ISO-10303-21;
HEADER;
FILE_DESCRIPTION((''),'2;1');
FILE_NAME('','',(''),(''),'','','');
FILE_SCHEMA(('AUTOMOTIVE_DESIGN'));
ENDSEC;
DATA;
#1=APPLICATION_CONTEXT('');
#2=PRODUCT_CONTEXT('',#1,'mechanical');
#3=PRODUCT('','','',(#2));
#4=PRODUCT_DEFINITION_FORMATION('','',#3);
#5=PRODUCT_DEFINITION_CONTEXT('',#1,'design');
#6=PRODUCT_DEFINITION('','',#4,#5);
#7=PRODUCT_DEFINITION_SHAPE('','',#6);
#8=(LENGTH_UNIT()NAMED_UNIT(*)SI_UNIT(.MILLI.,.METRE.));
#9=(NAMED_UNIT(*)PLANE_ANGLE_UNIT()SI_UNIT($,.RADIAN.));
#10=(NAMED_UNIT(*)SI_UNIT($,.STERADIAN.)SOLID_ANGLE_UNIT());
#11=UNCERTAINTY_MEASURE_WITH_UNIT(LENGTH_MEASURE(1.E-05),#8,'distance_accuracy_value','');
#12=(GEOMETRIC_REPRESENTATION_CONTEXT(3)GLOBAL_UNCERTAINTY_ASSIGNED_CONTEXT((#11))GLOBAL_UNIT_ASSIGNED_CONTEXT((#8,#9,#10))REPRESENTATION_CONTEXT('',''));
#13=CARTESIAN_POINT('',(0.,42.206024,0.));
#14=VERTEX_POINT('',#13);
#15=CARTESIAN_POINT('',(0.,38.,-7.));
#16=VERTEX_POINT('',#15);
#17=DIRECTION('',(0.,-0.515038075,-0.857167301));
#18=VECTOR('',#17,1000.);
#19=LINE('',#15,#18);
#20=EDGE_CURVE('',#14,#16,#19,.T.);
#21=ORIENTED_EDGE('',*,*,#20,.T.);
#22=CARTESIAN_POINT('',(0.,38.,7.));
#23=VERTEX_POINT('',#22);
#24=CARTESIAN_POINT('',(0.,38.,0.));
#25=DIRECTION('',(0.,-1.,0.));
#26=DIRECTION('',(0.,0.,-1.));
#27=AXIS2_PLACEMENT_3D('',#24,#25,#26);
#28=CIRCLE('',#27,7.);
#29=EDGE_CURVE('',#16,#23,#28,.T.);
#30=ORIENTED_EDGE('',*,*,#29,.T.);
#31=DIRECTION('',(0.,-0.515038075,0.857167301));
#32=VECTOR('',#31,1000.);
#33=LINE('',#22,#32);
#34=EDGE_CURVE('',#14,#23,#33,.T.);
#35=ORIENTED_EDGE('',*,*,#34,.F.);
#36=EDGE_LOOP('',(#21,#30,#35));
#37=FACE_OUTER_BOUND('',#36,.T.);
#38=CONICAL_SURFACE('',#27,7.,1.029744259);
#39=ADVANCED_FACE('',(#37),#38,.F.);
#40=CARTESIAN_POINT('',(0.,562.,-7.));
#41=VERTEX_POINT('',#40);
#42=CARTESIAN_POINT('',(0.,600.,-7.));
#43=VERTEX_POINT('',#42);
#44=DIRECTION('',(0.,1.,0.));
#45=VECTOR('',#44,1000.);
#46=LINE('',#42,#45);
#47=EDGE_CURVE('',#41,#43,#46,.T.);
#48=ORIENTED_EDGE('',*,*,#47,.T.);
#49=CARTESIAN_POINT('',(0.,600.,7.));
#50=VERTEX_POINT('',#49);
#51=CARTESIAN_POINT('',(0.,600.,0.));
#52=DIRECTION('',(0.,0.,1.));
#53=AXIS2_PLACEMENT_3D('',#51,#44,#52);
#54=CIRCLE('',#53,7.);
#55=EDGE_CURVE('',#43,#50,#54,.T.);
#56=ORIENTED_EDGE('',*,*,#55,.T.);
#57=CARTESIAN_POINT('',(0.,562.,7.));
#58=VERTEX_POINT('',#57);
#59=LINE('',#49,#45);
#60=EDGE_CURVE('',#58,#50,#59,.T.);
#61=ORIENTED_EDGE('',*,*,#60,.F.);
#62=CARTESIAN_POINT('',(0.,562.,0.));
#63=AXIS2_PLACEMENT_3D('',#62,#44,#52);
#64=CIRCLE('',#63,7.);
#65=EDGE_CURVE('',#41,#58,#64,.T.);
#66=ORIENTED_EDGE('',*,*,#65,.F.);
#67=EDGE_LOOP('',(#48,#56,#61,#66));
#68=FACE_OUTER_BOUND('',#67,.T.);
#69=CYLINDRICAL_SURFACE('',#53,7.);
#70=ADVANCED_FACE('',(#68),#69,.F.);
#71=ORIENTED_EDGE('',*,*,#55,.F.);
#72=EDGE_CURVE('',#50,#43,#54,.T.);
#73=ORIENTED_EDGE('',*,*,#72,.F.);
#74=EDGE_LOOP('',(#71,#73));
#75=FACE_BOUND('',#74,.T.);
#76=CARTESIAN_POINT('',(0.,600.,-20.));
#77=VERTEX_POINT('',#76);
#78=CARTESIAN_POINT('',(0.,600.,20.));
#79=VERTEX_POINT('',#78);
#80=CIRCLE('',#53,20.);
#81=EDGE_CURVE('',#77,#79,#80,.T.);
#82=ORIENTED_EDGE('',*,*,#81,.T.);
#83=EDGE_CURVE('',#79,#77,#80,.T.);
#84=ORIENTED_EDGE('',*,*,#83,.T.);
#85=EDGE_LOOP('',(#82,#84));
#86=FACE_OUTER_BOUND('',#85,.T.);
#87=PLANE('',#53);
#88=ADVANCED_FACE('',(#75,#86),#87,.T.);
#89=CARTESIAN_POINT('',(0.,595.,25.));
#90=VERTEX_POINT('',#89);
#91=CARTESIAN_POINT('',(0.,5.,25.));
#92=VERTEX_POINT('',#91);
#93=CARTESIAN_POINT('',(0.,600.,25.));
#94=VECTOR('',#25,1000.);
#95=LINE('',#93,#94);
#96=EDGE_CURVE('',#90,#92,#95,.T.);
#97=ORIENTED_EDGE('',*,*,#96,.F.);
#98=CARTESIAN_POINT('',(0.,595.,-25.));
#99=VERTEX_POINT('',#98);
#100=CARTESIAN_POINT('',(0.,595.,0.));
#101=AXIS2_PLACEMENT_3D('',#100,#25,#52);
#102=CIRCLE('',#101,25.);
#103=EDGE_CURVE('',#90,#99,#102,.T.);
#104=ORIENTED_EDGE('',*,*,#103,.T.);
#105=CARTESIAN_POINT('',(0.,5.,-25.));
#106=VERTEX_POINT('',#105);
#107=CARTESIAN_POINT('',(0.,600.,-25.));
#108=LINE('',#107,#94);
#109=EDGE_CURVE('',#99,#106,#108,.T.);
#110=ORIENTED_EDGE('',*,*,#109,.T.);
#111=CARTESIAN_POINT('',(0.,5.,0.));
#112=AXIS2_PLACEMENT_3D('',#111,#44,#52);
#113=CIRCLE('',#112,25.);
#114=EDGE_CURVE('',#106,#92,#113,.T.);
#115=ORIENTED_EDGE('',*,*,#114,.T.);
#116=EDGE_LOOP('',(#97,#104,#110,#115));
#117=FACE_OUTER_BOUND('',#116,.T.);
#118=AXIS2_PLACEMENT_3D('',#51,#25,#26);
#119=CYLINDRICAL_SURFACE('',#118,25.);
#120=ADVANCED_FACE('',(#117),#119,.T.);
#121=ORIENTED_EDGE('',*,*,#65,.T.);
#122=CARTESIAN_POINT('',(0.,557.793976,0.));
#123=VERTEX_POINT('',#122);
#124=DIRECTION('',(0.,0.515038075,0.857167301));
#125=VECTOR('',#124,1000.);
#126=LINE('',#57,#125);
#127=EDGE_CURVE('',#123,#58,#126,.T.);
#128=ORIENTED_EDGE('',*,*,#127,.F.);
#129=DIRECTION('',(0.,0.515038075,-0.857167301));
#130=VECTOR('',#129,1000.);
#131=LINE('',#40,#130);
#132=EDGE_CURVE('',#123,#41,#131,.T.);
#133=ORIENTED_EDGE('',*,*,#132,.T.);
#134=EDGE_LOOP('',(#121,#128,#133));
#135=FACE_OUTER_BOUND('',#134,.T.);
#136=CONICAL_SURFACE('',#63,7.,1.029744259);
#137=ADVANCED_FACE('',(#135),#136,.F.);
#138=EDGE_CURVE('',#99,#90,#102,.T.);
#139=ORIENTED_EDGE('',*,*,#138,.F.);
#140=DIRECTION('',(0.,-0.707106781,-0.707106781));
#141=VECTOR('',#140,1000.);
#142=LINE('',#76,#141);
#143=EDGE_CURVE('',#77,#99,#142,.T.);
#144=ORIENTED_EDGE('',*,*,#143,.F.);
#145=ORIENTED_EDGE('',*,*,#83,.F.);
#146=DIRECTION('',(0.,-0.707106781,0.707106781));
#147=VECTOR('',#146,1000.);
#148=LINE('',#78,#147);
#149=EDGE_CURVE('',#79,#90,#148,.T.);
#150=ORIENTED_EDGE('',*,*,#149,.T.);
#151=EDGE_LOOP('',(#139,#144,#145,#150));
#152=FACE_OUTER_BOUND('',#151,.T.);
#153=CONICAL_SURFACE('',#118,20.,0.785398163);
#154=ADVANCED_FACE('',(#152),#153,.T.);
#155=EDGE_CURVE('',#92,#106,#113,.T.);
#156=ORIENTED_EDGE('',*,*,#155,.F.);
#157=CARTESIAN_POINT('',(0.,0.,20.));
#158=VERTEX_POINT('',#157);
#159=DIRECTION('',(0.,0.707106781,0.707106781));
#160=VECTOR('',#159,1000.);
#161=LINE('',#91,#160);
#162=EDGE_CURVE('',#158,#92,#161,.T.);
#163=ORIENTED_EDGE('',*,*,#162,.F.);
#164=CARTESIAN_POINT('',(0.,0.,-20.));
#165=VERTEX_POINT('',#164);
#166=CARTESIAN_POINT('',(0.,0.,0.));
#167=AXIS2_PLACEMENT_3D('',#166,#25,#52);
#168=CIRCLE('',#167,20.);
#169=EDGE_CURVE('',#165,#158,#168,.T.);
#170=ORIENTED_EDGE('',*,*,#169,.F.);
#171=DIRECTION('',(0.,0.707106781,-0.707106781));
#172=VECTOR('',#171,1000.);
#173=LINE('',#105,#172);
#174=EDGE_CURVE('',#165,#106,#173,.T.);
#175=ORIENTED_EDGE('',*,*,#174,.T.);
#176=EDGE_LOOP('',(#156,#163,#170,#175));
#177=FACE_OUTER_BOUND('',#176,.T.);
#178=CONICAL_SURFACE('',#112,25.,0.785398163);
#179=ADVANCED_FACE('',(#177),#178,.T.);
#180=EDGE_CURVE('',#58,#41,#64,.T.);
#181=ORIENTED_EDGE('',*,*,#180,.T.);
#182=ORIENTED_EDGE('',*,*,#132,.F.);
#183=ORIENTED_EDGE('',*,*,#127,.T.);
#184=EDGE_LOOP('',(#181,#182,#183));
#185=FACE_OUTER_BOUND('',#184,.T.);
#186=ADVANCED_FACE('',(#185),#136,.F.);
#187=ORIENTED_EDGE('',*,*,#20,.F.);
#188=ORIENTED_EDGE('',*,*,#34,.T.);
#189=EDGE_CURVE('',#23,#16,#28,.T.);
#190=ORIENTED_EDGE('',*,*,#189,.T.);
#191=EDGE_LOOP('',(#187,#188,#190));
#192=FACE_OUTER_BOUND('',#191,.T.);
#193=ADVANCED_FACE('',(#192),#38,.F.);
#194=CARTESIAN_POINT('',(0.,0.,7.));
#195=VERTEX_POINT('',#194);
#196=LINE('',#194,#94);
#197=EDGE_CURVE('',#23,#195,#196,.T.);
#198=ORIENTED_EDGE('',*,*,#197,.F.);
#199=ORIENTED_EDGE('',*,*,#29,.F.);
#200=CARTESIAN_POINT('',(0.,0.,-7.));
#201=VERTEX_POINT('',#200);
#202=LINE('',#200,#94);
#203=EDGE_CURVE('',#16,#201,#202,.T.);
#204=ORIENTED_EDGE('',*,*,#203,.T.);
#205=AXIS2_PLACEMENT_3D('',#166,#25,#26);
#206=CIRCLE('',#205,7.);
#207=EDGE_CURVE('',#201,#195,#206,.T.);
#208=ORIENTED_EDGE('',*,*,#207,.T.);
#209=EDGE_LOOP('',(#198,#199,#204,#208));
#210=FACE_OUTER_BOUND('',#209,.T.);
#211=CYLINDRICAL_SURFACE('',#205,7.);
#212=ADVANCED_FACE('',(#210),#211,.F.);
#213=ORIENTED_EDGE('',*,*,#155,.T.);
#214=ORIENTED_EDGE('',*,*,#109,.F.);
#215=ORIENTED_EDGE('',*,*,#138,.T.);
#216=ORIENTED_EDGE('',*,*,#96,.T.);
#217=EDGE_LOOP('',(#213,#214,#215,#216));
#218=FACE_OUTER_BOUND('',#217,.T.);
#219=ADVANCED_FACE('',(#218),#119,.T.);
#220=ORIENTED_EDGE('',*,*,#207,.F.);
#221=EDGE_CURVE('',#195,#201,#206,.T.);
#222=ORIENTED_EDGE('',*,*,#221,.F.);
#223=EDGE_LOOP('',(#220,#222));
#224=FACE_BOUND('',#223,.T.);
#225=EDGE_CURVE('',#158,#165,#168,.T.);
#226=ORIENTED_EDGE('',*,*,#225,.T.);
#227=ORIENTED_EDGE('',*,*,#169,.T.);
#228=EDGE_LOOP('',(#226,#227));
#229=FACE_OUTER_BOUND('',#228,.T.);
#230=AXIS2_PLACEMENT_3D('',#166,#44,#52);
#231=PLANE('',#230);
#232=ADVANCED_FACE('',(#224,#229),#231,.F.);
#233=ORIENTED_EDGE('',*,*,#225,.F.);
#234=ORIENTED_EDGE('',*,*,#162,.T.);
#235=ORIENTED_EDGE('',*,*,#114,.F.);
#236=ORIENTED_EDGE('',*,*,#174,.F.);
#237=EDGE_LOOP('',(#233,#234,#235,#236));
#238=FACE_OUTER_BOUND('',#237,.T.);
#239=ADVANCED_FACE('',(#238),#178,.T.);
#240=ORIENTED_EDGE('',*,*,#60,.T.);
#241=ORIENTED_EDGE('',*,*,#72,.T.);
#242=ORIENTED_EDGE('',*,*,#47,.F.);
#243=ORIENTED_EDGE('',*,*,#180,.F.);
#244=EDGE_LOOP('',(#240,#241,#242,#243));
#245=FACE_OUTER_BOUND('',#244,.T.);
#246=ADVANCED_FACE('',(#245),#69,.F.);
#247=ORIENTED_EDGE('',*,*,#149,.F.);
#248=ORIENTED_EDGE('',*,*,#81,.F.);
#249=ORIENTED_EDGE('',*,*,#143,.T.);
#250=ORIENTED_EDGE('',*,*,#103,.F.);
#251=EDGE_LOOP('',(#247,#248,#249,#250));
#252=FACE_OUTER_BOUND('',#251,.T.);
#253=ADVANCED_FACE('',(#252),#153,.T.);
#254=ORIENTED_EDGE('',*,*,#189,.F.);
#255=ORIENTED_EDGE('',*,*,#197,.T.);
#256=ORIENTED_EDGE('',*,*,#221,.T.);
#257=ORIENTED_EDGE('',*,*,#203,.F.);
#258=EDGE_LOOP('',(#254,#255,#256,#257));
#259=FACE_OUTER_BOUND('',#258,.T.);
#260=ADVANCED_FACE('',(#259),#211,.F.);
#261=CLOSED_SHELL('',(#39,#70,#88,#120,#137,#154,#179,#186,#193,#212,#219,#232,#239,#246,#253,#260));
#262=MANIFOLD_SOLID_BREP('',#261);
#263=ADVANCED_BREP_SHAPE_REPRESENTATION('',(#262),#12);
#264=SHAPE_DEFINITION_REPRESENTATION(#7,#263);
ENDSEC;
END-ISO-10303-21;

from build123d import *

# Parameters (mm, degrees)
SKETCH1_R              = 25
BOSS_EXTRUDE1_DEPTH    = 600
CHAMFER1_SIZE          = 5
M16_TAPPED_HOLE1_D     = 14
M16_TAPPED_HOLE1_DEPTH = 38
M16_TAPPED_HOLE1_TIP   = 4.206024333
M16_TAPPED_HOLE2_D     = 14
M16_TAPPED_HOLE2_DEPTH = 38
M16_TAPPED_HOLE2_TIP   = 4.206024333


with BuildPart() as part:
    # Sketch1 → Boss-Extrude1 (new body)
    with BuildSketch(Plane(origin=(0, 0, 0), x_dir=(1, 0, 0), z_dir=(0, 1, 0))):
        with Locations(Location((0, 0, 0), (0, 0, 270))):
            Circle(SKETCH1_R)
    extrude(amount=BOSS_EXTRUDE1_DEPTH)

    # Chamfer1
    chamfer1_edges = [part.edges().sort_by_distance(p)[0] for p in [
        (0, 0, -25),
        (0, 600, -25),
    ]]
    chamfer(chamfer1_edges, length=CHAMFER1_SIZE)

    # M16 Tapped Hole1
    with Locations(Plane(origin=(0, 600, 0), x_dir=(1, 0, 0), z_dir=(0, 1, 0))):
        with Locations((0, 0)):
            Hole(M16_TAPPED_HOLE1_D / 2, depth=M16_TAPPED_HOLE1_DEPTH)
            with Locations((0, 0, -(M16_TAPPED_HOLE1_DEPTH + M16_TAPPED_HOLE1_TIP / 2))):  # 118° drill point
                Cone(0, M16_TAPPED_HOLE1_D / 2, M16_TAPPED_HOLE1_TIP, mode=Mode.SUBTRACT)

    # M16 Tapped Hole2
    with Locations(Plane(origin=(0, 0, 0), x_dir=(-1, 0, 0), z_dir=(0, -1, 0))):
        with Locations((0, 0)):
            Hole(M16_TAPPED_HOLE2_D / 2, depth=M16_TAPPED_HOLE2_DEPTH)
            with Locations((0, 0, -(M16_TAPPED_HOLE2_DEPTH + M16_TAPPED_HOLE2_TIP / 2))):  # 118° drill point
                Cone(0, M16_TAPPED_HOLE2_D / 2, M16_TAPPED_HOLE2_TIP, mode=Mode.SUBTRACT)


solid = part.part
